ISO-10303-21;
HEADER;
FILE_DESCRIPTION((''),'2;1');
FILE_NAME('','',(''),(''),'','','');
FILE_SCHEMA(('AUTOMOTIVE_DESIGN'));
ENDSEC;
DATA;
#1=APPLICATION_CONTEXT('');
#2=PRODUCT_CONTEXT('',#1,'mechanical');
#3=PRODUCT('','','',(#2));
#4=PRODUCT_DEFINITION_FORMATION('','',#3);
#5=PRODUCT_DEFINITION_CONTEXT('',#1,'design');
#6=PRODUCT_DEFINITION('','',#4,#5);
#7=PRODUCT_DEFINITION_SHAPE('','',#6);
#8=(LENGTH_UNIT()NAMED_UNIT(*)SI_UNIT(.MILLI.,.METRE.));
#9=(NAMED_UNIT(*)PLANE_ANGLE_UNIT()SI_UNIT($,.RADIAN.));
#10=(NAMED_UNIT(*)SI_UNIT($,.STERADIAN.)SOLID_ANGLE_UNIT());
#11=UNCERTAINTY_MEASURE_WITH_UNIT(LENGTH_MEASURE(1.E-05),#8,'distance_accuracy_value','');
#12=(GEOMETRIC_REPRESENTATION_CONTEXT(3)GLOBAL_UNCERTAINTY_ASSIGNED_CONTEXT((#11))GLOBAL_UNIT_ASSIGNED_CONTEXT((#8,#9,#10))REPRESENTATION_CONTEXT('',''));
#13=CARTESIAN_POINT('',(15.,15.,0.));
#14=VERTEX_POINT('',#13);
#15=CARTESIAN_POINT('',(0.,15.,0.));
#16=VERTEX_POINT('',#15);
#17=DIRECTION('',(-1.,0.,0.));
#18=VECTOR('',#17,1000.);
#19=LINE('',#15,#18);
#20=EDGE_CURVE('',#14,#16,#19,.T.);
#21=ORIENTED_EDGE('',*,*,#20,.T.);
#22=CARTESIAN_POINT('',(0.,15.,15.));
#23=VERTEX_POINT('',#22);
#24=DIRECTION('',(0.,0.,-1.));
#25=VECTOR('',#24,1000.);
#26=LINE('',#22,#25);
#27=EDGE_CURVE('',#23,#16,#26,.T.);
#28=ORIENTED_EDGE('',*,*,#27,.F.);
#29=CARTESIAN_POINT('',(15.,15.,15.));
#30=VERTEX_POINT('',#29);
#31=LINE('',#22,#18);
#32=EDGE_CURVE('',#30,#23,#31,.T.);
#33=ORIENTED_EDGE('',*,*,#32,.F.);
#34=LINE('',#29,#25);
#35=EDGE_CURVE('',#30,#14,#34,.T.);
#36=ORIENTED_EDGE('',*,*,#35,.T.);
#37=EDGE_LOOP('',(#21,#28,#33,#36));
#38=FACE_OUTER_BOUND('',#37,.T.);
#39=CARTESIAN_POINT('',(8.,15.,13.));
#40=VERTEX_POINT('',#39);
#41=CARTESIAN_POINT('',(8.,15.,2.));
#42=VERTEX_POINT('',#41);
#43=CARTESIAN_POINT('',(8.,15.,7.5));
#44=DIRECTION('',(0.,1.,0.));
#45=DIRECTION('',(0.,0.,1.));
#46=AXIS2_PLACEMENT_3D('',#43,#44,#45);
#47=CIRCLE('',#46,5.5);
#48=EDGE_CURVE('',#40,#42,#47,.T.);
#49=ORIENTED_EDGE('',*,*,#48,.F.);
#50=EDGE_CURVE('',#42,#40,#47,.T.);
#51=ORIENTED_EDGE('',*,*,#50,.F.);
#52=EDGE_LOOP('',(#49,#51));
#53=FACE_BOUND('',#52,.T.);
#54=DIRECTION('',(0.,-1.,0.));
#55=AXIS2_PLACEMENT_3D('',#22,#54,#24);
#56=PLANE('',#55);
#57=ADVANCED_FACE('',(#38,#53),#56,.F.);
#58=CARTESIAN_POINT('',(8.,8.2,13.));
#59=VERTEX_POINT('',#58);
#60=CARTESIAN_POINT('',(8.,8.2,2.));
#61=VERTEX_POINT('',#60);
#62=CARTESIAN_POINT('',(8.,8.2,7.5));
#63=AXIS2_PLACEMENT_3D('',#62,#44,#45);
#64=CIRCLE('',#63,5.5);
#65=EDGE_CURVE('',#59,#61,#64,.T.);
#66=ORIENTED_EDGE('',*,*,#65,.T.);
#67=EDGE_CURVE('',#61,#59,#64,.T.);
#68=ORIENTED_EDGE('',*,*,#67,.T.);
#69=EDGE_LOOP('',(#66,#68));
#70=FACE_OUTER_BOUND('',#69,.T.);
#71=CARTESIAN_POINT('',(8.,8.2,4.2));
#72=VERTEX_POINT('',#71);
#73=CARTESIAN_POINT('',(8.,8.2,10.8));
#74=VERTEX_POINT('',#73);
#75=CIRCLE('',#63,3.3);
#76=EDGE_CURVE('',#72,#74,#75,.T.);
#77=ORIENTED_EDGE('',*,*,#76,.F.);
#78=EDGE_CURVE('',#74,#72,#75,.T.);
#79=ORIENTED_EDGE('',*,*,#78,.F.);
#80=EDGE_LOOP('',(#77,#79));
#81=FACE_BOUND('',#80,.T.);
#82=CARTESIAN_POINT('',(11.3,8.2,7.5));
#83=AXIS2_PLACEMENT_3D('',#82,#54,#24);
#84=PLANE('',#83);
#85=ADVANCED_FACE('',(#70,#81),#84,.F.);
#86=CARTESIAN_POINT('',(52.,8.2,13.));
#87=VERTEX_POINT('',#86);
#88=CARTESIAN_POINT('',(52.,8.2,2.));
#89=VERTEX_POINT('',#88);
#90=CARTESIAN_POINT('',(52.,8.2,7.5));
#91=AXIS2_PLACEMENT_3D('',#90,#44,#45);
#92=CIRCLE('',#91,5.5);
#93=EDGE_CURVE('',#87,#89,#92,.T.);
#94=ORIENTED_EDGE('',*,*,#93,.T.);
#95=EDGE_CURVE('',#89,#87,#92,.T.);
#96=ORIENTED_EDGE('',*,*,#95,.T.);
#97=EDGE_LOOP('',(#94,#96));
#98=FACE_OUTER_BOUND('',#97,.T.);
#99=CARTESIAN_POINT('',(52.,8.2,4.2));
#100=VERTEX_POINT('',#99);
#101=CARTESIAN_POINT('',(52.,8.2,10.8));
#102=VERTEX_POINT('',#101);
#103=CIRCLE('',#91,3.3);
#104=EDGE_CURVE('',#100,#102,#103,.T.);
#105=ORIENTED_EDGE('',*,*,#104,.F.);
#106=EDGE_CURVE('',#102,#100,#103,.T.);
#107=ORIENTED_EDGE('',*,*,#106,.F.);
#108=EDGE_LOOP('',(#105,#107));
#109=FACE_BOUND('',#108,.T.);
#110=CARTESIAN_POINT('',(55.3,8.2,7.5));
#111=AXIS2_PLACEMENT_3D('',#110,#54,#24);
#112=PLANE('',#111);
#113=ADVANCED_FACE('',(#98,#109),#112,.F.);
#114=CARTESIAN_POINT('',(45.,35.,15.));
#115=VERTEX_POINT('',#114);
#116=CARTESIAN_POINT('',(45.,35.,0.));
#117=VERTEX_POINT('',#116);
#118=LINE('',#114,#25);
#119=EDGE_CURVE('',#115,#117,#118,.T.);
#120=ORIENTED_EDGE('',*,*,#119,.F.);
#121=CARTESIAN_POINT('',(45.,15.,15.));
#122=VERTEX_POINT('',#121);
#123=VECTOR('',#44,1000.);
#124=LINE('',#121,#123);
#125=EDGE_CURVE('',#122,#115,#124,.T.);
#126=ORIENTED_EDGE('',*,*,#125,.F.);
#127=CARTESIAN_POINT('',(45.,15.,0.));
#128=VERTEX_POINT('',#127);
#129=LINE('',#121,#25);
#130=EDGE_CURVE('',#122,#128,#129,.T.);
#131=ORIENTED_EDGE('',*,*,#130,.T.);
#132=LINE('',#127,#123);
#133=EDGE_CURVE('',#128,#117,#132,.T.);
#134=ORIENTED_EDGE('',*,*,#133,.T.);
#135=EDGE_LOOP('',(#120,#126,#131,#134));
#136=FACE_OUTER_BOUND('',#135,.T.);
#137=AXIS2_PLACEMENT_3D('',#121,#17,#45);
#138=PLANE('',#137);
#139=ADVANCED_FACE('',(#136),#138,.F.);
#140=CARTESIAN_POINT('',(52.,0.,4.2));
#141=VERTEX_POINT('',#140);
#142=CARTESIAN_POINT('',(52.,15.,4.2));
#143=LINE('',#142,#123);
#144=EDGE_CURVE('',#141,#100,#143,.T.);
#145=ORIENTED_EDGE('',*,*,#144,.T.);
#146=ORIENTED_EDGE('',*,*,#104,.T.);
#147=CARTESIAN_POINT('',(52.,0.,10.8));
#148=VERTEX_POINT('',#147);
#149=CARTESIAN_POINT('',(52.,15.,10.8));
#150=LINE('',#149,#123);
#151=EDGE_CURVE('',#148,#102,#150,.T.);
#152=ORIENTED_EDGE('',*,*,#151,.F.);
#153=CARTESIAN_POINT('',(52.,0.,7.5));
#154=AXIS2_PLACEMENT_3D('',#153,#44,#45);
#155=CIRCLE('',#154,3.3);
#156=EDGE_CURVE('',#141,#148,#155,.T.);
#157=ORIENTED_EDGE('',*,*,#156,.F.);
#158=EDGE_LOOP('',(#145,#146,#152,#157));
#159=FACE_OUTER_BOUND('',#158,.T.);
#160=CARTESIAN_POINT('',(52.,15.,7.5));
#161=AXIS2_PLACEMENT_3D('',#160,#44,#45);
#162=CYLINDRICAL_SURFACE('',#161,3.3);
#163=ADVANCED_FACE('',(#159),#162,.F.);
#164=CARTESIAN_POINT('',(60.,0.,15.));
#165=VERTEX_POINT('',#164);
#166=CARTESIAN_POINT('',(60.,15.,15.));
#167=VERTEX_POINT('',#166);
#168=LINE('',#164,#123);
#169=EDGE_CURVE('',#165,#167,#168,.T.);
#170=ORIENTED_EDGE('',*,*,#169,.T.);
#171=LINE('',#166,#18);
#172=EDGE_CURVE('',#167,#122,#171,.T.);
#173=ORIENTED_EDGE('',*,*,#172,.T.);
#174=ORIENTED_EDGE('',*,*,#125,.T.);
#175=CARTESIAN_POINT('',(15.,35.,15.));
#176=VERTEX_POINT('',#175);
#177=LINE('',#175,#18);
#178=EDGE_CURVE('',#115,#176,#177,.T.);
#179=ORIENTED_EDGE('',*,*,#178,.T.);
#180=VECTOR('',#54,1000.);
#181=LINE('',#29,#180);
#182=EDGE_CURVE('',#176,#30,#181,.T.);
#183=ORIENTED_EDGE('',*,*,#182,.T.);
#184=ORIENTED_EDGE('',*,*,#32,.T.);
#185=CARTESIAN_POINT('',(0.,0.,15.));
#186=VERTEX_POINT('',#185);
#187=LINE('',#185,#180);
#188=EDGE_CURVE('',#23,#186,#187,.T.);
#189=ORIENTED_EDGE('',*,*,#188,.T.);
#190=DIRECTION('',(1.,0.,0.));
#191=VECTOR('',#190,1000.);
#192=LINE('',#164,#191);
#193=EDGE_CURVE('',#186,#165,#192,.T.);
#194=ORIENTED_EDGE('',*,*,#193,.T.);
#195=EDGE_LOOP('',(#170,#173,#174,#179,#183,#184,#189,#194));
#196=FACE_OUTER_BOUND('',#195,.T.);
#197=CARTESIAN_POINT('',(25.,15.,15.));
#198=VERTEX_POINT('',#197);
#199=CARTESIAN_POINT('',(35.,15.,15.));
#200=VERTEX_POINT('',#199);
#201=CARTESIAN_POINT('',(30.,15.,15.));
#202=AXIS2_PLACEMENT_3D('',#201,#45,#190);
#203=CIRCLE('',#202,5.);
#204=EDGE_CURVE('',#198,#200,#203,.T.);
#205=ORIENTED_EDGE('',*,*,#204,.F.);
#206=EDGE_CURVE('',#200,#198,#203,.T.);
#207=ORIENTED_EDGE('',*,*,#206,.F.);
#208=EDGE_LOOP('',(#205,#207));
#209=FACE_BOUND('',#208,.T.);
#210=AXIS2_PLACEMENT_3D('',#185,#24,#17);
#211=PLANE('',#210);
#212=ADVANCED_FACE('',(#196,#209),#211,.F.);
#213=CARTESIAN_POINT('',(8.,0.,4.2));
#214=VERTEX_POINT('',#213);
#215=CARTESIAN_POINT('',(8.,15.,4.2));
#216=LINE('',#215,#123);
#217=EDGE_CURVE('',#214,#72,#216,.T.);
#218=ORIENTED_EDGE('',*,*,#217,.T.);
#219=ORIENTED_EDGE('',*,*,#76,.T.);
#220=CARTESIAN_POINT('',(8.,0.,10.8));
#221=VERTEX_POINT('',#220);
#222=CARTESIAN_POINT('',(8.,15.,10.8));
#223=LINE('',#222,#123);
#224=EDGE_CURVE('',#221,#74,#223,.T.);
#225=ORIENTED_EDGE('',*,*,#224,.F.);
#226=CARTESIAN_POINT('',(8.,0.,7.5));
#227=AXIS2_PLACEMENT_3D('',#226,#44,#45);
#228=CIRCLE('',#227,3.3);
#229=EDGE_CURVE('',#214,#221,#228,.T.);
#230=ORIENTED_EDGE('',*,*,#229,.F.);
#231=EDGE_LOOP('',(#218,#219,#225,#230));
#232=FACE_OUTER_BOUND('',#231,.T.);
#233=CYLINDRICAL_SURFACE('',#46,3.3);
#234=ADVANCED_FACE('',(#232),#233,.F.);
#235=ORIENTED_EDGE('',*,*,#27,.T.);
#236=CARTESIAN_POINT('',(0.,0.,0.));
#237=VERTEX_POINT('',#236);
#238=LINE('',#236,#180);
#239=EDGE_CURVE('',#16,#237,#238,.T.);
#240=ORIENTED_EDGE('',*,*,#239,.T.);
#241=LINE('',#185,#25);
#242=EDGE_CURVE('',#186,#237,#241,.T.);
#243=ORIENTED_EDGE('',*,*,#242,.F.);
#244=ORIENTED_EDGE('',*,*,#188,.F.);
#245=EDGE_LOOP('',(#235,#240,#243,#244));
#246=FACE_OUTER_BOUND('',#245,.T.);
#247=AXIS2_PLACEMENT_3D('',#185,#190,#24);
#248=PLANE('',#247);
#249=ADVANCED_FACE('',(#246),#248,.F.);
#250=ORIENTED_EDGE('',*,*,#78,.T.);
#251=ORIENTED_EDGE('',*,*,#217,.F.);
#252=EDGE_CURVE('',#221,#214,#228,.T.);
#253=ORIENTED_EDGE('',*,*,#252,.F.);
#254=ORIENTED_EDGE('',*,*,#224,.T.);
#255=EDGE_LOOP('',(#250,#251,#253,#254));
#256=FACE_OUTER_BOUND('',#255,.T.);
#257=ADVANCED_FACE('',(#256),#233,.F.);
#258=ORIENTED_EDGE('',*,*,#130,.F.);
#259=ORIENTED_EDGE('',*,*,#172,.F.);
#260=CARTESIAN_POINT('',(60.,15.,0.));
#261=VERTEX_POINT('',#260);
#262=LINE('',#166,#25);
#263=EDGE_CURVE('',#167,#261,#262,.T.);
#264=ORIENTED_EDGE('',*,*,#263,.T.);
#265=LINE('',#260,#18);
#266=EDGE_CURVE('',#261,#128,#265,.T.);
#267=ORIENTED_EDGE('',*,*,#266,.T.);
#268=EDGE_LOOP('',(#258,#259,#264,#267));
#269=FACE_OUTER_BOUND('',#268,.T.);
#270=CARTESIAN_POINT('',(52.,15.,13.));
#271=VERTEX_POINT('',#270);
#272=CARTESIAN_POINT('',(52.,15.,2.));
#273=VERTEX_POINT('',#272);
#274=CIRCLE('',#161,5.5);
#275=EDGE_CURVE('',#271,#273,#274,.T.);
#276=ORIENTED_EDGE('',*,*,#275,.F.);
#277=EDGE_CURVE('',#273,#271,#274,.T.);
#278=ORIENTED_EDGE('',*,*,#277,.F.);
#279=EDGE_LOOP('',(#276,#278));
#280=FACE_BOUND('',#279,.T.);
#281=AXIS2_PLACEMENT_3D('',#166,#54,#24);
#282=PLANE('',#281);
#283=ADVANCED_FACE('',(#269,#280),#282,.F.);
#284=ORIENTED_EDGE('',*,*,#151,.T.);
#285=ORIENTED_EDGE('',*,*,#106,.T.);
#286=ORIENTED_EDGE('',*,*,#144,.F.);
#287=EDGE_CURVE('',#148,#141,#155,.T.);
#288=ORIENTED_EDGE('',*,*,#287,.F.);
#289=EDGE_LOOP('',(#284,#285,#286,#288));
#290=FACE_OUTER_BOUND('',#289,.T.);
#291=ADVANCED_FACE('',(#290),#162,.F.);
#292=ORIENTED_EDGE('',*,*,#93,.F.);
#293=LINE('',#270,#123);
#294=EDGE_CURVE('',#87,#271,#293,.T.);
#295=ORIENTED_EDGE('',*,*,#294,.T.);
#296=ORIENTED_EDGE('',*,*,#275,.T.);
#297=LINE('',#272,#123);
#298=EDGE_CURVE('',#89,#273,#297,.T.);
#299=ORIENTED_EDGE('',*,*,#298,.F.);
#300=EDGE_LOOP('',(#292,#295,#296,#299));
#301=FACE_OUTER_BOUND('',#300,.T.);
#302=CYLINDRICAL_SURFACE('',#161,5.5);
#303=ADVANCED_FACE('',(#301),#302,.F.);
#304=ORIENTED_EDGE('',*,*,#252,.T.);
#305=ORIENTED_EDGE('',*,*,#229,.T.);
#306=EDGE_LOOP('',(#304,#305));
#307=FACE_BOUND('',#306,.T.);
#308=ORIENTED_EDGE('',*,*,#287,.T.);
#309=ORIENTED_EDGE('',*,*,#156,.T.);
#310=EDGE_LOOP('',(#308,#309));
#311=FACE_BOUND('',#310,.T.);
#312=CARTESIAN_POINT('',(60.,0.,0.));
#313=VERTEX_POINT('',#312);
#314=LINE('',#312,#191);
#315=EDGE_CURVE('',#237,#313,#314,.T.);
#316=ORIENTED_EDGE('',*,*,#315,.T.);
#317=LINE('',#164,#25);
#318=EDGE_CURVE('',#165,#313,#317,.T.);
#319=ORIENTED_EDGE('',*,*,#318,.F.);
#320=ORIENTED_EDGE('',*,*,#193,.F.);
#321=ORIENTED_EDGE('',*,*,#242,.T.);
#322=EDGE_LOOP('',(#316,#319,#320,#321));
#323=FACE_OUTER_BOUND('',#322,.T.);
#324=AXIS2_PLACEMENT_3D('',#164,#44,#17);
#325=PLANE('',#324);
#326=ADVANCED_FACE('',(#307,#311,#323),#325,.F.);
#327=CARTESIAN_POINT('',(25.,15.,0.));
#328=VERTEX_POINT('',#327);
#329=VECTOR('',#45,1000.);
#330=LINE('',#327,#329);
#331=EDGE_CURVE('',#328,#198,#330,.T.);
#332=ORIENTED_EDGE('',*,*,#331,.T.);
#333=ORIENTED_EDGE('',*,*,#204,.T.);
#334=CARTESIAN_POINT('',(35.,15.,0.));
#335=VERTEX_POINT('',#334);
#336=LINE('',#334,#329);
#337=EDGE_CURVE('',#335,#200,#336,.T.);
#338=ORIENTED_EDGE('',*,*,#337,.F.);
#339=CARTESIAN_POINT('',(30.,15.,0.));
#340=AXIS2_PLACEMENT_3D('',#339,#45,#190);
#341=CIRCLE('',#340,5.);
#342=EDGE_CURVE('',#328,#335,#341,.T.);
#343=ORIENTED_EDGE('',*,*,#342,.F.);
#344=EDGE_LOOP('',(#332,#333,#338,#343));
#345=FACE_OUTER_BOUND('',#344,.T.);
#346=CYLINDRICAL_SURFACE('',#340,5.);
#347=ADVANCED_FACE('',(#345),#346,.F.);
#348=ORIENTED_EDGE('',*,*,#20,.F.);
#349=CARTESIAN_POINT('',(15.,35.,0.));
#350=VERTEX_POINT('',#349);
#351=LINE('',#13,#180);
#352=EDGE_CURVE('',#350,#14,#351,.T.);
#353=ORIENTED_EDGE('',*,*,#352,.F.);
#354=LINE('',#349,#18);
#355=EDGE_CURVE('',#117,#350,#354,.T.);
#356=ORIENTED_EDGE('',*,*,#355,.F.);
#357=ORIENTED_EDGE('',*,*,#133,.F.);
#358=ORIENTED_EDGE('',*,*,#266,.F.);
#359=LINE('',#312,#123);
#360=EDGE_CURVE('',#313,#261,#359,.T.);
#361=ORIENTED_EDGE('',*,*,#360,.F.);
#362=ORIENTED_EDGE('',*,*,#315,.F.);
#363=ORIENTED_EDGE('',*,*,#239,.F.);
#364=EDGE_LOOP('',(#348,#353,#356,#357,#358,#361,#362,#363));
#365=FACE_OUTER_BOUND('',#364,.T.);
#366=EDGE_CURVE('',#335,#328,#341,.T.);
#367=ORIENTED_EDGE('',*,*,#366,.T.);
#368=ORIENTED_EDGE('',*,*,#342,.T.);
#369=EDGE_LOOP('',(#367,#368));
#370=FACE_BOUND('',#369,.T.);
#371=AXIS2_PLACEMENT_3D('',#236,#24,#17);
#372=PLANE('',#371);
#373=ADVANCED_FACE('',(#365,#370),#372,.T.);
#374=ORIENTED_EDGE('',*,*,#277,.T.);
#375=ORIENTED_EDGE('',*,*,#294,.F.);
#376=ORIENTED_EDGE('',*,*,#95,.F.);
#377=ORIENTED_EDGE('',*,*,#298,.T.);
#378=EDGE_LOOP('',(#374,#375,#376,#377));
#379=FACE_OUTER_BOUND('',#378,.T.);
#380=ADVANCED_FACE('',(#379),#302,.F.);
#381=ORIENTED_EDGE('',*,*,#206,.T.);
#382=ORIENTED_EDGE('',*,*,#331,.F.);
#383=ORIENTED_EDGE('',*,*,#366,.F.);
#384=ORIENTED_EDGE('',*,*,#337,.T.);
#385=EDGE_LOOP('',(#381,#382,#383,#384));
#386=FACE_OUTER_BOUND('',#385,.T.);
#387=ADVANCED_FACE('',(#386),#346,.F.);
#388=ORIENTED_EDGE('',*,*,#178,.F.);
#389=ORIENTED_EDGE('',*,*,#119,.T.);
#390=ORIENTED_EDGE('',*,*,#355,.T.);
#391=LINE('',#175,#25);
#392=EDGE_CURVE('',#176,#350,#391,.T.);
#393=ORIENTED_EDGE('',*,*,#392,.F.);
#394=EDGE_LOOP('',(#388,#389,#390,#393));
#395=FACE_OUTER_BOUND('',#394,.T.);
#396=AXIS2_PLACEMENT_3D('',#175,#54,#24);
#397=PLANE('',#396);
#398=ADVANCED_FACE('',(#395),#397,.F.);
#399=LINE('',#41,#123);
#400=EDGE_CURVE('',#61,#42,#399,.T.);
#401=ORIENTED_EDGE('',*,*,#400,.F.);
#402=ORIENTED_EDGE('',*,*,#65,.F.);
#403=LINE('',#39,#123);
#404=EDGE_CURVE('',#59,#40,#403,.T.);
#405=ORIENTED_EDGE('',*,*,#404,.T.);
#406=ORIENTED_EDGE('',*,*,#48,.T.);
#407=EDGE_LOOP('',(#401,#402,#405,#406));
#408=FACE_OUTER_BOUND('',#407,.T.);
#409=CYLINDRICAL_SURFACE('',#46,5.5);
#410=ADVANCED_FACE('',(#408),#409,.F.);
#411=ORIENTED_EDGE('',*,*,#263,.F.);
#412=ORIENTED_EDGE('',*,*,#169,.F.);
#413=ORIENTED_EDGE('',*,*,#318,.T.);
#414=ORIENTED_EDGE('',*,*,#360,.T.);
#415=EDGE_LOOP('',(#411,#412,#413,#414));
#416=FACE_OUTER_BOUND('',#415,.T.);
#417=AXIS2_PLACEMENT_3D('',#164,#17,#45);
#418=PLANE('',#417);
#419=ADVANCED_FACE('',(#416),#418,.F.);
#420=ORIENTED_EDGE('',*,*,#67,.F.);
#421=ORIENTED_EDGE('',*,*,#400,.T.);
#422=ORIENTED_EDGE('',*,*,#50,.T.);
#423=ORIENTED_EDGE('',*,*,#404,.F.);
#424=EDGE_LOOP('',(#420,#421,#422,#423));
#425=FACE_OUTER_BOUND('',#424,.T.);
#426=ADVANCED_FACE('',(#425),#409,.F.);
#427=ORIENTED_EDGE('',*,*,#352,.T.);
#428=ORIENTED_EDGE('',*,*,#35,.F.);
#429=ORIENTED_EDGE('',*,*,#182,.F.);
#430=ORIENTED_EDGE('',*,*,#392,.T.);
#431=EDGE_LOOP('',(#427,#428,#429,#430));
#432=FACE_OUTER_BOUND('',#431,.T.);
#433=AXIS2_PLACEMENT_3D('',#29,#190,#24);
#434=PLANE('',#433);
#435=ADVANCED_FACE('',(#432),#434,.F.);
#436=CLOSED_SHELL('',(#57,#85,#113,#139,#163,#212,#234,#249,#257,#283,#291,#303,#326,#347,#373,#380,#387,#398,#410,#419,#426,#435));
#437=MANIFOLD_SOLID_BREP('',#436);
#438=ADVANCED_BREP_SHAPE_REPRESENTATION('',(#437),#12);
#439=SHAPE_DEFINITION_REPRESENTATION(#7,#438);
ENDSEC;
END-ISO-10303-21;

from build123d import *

# Parameters (mm, degrees)
BOSS_EXTRUDE1_DEPTH                                  = 15
SKETCH2_R                                            = 5
CUT_EXTRUDE1_DEPTH                                   = 72.063352018
CBORE_FOR_M6_HEXAGON_SOCKET_HEAD_CAP_SCR_D           = 6.6
CBORE_FOR_M6_HEXAGON_SOCKET_HEAD_CAP_SCR_CBORE_D     = 11
CBORE_FOR_M6_HEXAGON_SOCKET_HEAD_CAP_SCR_CBORE_DEPTH = 6.8


with BuildPart() as part:
    # Sketch1 → Boss-Extrude1 (new body)
    with BuildSketch(Plane.XY):
        Polygon((0, 0), (0, 15), (15, 15), (15, 35), (45, 35), (45, 15), (60, 15), (60, 0), align=None)
    extrude(amount=BOSS_EXTRUDE1_DEPTH)

    # Sketch2 → Cut-Extrude1 (cut, through all)
    with BuildSketch(Plane.XY.offset(15)):
        with Locations((30, 15)):
            Circle(SKETCH2_R)
    extrude(amount=-CUT_EXTRUDE1_DEPTH, mode=Mode.SUBTRACT)

    # CBORE for M6 Hexagon socket head cap screws1 (through all)
    with Locations(Plane(origin=(8, 15, 7.5), x_dir=(0, 0, 1), z_dir=(0, 1, 0))):
        with Locations((0, 0), (0, 44)):
            CounterBoreHole(CBORE_FOR_M6_HEXAGON_SOCKET_HEAD_CAP_SCR_D / 2, CBORE_FOR_M6_HEXAGON_SOCKET_HEAD_CAP_SCR_CBORE_D / 2, CBORE_FOR_M6_HEXAGON_SOCKET_HEAD_CAP_SCR_CBORE_DEPTH)


solid = part.part
